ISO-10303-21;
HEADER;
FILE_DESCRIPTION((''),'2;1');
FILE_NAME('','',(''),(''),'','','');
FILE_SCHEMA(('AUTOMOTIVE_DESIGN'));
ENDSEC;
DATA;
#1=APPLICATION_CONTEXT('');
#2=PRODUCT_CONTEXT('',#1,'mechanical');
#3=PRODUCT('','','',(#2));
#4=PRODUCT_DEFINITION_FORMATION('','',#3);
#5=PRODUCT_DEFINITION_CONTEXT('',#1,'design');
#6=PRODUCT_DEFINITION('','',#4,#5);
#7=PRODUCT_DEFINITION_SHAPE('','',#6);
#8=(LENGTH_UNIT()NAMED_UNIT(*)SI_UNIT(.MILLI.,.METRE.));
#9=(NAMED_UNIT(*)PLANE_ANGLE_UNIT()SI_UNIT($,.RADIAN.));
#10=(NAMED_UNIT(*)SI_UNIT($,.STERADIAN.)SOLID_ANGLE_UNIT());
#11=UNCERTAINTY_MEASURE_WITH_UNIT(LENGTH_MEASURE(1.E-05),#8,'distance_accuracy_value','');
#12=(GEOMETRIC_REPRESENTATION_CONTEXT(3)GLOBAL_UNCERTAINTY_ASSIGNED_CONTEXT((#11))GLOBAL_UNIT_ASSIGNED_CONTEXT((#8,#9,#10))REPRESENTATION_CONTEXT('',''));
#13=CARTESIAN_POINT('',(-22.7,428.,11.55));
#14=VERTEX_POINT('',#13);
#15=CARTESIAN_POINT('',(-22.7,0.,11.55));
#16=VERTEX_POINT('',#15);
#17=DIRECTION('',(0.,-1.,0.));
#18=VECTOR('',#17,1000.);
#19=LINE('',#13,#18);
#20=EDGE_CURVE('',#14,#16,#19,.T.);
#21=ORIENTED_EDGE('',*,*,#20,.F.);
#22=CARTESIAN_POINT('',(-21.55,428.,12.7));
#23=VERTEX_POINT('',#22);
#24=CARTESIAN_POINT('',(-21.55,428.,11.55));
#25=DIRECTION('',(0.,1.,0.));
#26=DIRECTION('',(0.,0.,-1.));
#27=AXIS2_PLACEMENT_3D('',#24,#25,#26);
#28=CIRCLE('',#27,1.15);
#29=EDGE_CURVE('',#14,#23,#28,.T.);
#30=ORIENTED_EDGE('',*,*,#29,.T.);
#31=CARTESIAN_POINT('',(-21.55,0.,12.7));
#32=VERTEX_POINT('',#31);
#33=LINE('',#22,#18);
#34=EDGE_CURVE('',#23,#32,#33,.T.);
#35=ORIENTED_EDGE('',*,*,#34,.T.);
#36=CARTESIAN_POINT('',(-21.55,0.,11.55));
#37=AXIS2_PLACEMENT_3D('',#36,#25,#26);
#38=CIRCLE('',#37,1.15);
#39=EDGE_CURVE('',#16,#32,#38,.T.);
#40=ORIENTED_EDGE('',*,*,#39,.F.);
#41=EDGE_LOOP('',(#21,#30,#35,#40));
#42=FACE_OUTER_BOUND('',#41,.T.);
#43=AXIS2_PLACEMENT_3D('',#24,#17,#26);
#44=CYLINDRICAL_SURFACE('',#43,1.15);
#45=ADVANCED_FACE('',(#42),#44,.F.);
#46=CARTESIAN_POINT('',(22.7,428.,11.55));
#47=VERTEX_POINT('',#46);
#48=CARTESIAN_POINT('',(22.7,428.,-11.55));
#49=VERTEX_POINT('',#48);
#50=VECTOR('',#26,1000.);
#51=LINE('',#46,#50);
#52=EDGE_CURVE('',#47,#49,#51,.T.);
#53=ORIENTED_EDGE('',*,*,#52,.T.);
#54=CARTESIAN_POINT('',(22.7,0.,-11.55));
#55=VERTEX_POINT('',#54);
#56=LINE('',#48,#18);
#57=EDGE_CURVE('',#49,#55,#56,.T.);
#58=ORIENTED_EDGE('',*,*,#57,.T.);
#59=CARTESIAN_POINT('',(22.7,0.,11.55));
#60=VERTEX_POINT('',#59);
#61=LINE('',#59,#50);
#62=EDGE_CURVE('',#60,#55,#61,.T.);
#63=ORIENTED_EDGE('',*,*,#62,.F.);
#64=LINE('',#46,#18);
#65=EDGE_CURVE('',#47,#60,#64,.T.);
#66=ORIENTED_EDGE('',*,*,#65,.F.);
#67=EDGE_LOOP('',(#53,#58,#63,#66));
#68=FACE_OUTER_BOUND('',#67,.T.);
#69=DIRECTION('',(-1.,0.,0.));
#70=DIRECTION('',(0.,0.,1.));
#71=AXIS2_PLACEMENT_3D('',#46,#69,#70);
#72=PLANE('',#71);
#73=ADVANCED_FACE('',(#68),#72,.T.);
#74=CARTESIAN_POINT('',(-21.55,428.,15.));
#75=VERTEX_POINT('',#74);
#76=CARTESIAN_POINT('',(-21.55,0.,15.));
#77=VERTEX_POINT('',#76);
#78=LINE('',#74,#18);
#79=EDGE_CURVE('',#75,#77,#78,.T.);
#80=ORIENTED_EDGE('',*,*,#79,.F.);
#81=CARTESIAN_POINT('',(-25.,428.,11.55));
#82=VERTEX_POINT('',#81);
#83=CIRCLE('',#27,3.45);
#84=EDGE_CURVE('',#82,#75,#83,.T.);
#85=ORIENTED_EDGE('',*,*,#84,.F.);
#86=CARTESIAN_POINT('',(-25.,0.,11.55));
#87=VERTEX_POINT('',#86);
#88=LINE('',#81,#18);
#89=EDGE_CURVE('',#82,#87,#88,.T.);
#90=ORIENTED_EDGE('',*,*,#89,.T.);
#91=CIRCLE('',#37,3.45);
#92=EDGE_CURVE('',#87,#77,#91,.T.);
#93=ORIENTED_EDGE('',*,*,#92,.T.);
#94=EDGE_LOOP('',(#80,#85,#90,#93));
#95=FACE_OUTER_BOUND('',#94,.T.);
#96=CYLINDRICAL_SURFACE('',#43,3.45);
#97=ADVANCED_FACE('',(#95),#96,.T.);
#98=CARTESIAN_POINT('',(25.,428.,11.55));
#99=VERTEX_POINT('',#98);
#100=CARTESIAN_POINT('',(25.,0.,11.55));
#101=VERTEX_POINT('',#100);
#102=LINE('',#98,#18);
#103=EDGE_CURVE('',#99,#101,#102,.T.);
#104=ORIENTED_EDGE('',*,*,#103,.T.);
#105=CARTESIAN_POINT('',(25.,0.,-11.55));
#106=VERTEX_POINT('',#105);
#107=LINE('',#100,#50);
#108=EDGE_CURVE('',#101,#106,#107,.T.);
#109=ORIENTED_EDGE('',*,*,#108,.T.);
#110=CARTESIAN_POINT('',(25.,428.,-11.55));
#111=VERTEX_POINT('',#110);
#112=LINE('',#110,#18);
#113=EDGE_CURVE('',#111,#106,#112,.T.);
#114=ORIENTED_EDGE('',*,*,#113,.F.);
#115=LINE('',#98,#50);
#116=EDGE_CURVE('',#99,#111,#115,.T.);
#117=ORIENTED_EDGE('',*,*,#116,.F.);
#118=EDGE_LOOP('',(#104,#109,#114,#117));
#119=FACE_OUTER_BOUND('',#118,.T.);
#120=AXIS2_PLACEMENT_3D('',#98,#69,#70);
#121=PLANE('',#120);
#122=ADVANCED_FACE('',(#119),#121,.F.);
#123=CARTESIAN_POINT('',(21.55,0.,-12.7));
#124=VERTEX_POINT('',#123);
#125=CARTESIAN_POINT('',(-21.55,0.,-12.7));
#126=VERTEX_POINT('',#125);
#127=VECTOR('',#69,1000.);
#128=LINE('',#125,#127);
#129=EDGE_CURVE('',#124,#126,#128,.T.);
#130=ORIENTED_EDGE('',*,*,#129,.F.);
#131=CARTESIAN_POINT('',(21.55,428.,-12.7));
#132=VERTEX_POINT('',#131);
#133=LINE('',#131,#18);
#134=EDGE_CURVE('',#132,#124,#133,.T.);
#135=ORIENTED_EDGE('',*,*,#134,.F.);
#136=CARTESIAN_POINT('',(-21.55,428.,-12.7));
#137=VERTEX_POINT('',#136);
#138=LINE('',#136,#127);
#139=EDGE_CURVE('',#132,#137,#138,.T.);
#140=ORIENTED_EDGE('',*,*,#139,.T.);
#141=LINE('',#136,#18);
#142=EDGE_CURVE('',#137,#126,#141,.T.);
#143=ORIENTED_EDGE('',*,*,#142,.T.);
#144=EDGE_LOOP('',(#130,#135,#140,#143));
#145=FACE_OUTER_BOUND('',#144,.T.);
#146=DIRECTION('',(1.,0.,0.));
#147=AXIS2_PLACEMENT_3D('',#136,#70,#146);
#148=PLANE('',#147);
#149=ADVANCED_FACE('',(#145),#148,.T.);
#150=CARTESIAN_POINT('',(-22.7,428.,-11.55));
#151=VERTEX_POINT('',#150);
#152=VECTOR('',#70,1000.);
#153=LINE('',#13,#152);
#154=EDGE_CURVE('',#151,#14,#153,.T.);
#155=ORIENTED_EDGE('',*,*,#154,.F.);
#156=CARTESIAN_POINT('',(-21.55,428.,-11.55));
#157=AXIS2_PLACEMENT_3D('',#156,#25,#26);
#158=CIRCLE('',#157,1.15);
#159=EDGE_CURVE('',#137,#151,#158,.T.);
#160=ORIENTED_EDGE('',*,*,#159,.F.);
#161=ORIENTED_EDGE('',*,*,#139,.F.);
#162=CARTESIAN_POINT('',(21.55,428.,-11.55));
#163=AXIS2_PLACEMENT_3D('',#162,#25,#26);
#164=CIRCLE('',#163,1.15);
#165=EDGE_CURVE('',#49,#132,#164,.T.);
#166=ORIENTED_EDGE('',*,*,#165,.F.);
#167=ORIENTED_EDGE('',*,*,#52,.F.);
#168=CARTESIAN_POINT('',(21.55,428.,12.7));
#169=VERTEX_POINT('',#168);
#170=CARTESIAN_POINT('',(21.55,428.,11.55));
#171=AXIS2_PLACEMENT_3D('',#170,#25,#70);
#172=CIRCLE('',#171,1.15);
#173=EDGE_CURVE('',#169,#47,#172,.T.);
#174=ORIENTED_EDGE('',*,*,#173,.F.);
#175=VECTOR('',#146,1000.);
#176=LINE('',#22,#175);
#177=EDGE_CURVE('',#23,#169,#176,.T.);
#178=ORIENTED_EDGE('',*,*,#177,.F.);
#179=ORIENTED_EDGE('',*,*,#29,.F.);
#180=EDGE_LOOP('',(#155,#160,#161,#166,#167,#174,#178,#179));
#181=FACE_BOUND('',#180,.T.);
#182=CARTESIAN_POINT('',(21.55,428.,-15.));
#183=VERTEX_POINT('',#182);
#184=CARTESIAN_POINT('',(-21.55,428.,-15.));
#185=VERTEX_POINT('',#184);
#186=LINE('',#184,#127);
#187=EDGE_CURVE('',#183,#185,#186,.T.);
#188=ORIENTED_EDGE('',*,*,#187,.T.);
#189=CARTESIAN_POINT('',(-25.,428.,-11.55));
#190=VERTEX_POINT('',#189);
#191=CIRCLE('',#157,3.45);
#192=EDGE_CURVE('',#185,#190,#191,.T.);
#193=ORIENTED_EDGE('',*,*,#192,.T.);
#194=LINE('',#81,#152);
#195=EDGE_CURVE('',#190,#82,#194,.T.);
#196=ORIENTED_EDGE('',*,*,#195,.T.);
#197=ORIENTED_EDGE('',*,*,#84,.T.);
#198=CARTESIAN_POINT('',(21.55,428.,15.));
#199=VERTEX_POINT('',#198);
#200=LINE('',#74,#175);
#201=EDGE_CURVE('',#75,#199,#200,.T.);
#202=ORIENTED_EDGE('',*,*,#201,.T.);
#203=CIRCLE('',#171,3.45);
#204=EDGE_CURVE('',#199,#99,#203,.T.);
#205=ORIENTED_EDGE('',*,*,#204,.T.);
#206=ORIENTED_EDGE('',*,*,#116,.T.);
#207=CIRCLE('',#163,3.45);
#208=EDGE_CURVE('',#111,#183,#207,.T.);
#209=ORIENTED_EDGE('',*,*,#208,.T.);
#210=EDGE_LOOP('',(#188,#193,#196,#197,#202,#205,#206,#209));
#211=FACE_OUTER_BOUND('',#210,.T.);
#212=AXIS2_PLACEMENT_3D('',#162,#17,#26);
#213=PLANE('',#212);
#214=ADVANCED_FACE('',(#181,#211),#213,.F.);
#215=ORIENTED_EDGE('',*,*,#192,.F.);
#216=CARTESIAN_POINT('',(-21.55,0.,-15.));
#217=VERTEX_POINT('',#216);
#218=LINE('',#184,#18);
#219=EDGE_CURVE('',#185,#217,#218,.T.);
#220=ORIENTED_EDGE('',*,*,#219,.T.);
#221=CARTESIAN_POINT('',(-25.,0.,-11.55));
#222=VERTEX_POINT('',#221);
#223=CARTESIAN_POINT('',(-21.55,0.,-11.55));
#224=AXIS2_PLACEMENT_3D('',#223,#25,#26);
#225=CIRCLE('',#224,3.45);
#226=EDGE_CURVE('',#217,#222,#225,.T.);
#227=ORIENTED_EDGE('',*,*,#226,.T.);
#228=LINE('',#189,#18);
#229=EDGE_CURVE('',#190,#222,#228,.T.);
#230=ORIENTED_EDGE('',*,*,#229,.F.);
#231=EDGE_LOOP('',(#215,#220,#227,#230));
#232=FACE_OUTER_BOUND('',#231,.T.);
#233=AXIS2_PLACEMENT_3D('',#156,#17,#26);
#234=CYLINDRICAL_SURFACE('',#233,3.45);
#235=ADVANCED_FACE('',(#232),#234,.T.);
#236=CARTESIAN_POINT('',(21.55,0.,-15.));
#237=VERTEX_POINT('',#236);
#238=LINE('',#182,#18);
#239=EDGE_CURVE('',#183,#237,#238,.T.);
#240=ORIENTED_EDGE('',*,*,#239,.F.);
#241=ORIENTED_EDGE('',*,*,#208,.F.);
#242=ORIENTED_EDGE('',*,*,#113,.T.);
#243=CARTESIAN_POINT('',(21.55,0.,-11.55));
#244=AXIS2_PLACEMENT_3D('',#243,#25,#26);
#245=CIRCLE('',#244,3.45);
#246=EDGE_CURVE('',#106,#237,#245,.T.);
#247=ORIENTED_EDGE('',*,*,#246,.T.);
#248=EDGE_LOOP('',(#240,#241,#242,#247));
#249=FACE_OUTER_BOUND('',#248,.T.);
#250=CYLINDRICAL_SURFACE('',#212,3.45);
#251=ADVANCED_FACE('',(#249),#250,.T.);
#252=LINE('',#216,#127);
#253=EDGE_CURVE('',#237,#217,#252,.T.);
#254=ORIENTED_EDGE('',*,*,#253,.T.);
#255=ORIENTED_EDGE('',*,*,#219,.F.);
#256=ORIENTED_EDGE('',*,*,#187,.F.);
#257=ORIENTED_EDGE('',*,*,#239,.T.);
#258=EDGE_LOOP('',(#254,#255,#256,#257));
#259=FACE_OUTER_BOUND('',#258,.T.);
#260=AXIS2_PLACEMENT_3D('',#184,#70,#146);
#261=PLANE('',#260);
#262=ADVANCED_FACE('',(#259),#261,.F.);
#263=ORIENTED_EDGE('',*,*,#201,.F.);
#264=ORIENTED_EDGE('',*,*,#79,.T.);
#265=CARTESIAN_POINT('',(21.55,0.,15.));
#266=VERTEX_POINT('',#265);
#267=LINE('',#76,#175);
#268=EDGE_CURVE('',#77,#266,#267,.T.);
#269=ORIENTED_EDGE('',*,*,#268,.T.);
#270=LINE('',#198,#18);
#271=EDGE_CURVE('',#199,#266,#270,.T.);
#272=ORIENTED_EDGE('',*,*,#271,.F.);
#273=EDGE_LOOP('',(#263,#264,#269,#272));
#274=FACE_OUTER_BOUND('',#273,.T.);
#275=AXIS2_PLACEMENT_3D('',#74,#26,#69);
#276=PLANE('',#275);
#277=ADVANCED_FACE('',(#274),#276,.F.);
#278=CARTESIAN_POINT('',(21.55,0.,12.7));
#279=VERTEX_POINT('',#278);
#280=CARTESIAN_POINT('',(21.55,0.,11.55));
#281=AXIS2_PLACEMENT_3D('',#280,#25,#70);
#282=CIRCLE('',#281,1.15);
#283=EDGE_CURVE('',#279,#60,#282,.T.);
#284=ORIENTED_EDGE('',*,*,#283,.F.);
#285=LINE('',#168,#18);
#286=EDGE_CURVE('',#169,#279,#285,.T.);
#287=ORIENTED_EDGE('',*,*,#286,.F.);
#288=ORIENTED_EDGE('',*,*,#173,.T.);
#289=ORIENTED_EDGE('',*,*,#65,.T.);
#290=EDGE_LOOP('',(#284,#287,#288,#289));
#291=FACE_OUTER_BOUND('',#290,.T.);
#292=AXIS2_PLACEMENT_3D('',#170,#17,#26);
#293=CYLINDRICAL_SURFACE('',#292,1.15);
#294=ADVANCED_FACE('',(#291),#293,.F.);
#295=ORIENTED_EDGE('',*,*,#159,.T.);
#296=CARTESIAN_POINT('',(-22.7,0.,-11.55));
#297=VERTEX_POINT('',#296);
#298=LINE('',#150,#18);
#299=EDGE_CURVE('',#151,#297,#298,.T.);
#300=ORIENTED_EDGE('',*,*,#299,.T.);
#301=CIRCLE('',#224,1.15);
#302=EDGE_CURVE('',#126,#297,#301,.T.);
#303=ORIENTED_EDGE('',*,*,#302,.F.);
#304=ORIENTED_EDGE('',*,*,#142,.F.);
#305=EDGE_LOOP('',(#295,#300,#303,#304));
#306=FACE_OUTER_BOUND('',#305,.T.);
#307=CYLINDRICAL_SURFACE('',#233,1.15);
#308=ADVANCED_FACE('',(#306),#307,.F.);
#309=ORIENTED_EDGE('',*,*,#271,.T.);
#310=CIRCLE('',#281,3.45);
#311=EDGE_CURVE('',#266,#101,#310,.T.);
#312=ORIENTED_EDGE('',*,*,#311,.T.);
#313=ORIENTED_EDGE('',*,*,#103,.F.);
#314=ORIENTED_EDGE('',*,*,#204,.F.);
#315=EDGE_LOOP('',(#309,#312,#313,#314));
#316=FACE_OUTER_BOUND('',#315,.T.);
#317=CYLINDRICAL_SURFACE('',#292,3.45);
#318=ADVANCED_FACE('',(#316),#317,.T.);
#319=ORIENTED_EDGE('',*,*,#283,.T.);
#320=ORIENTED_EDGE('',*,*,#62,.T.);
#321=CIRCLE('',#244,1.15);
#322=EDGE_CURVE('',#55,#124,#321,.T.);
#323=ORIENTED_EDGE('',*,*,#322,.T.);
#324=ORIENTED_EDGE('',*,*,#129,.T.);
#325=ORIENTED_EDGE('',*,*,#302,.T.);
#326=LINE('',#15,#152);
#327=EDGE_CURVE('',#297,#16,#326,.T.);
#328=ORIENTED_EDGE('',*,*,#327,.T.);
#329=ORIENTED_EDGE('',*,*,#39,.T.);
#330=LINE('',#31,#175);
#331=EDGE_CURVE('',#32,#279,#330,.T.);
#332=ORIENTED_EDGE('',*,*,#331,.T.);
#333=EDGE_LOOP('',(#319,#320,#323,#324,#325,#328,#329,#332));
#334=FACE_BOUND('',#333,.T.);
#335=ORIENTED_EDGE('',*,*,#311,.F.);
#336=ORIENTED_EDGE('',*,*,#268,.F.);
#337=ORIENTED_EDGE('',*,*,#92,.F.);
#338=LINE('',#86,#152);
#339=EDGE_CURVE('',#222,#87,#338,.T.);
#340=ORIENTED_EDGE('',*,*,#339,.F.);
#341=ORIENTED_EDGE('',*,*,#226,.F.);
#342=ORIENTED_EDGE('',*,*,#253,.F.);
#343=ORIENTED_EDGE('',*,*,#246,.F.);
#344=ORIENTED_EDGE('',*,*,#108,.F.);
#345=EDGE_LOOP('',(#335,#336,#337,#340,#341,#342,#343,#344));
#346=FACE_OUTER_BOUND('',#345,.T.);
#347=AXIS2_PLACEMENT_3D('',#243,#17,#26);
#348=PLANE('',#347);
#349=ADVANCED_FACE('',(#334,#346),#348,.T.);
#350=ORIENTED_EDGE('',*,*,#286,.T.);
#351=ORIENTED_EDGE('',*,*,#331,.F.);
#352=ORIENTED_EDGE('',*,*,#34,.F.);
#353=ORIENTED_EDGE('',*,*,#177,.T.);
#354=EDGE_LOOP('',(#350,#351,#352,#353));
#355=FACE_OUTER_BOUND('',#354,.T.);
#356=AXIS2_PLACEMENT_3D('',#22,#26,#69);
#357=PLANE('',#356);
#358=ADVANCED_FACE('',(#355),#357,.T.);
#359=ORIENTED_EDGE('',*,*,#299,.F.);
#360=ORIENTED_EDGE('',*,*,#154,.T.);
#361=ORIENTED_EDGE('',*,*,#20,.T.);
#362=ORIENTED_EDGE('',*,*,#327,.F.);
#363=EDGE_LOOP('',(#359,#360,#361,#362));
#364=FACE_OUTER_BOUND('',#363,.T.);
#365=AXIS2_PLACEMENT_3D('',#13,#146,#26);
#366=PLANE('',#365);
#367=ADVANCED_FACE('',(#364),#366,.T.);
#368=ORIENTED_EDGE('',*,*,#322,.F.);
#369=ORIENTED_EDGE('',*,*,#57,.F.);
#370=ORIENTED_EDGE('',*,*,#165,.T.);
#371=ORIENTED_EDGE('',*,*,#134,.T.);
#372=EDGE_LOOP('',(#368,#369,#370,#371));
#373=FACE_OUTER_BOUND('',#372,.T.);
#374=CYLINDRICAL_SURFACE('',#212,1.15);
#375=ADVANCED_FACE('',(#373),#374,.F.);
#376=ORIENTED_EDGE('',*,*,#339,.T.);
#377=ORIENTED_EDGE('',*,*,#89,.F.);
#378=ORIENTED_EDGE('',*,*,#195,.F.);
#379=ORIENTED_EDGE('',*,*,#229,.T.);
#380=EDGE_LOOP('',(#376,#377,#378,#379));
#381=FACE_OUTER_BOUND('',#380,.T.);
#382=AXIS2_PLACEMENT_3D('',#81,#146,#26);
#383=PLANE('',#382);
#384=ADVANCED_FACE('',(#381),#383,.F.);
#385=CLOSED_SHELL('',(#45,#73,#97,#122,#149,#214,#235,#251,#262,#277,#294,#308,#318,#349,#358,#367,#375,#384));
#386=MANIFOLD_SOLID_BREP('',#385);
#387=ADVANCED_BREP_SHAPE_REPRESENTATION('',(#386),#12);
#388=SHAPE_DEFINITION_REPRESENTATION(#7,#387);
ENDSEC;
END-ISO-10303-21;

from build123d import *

# Parameters (mm, degrees)
BOSS_EXTRUDE1_DEPTH = 428


with BuildPart() as part:
    # Sketch1 → Boss-Extrude1 (new body)
    with BuildSketch(Plane(origin=(0, 0, 0), x_dir=(1, 0, 0), z_dir=(0, 1, 0))):
        with BuildLine():
            Line((-21.55, -15), (21.55, -15))
            ThreePointArc((21.55, -15), (23.989518395, -13.989518395), (25, -11.55))
            Line((25, -11.55), (25, 11.55))
            ThreePointArc((25, 11.55), (23.989518395, 13.989518395), (21.55, 15))
            Line((21.55, 15), (-21.55, 15))
            ThreePointArc((-21.55, 15), (-23.989518395, 13.989518395), (-25, 11.55))
            Line((-25, 11.55), (-25, -11.55))
            ThreePointArc((-25, -11.55), (-23.989518395, -13.989518395), (-21.55, -15))
        make_face()
        with BuildLine():
            Line((-21.55, -12.7), (21.55, -12.7))
            ThreePointArc((21.55, -12.7), (22.363172798, -12.363172798), (22.7, -11.55))
            Line((22.7, -11.55), (22.7, 11.55))
            ThreePointArc((22.7, 11.55), (22.363172798, 12.363172798), (21.55, 12.7))
            Line((21.55, 12.7), (-21.55, 12.7))
            ThreePointArc((-21.55, 12.7), (-22.363172798, 12.363172798), (-22.7, 11.55))
            Line((-22.7, 11.55), (-22.7, -11.55))
            ThreePointArc((-22.7, -11.55), (-22.363172798, -12.363172798), (-21.55, -12.7))
        make_face(mode=Mode.SUBTRACT)
    extrude(amount=BOSS_EXTRUDE1_DEPTH)


solid = part.part
